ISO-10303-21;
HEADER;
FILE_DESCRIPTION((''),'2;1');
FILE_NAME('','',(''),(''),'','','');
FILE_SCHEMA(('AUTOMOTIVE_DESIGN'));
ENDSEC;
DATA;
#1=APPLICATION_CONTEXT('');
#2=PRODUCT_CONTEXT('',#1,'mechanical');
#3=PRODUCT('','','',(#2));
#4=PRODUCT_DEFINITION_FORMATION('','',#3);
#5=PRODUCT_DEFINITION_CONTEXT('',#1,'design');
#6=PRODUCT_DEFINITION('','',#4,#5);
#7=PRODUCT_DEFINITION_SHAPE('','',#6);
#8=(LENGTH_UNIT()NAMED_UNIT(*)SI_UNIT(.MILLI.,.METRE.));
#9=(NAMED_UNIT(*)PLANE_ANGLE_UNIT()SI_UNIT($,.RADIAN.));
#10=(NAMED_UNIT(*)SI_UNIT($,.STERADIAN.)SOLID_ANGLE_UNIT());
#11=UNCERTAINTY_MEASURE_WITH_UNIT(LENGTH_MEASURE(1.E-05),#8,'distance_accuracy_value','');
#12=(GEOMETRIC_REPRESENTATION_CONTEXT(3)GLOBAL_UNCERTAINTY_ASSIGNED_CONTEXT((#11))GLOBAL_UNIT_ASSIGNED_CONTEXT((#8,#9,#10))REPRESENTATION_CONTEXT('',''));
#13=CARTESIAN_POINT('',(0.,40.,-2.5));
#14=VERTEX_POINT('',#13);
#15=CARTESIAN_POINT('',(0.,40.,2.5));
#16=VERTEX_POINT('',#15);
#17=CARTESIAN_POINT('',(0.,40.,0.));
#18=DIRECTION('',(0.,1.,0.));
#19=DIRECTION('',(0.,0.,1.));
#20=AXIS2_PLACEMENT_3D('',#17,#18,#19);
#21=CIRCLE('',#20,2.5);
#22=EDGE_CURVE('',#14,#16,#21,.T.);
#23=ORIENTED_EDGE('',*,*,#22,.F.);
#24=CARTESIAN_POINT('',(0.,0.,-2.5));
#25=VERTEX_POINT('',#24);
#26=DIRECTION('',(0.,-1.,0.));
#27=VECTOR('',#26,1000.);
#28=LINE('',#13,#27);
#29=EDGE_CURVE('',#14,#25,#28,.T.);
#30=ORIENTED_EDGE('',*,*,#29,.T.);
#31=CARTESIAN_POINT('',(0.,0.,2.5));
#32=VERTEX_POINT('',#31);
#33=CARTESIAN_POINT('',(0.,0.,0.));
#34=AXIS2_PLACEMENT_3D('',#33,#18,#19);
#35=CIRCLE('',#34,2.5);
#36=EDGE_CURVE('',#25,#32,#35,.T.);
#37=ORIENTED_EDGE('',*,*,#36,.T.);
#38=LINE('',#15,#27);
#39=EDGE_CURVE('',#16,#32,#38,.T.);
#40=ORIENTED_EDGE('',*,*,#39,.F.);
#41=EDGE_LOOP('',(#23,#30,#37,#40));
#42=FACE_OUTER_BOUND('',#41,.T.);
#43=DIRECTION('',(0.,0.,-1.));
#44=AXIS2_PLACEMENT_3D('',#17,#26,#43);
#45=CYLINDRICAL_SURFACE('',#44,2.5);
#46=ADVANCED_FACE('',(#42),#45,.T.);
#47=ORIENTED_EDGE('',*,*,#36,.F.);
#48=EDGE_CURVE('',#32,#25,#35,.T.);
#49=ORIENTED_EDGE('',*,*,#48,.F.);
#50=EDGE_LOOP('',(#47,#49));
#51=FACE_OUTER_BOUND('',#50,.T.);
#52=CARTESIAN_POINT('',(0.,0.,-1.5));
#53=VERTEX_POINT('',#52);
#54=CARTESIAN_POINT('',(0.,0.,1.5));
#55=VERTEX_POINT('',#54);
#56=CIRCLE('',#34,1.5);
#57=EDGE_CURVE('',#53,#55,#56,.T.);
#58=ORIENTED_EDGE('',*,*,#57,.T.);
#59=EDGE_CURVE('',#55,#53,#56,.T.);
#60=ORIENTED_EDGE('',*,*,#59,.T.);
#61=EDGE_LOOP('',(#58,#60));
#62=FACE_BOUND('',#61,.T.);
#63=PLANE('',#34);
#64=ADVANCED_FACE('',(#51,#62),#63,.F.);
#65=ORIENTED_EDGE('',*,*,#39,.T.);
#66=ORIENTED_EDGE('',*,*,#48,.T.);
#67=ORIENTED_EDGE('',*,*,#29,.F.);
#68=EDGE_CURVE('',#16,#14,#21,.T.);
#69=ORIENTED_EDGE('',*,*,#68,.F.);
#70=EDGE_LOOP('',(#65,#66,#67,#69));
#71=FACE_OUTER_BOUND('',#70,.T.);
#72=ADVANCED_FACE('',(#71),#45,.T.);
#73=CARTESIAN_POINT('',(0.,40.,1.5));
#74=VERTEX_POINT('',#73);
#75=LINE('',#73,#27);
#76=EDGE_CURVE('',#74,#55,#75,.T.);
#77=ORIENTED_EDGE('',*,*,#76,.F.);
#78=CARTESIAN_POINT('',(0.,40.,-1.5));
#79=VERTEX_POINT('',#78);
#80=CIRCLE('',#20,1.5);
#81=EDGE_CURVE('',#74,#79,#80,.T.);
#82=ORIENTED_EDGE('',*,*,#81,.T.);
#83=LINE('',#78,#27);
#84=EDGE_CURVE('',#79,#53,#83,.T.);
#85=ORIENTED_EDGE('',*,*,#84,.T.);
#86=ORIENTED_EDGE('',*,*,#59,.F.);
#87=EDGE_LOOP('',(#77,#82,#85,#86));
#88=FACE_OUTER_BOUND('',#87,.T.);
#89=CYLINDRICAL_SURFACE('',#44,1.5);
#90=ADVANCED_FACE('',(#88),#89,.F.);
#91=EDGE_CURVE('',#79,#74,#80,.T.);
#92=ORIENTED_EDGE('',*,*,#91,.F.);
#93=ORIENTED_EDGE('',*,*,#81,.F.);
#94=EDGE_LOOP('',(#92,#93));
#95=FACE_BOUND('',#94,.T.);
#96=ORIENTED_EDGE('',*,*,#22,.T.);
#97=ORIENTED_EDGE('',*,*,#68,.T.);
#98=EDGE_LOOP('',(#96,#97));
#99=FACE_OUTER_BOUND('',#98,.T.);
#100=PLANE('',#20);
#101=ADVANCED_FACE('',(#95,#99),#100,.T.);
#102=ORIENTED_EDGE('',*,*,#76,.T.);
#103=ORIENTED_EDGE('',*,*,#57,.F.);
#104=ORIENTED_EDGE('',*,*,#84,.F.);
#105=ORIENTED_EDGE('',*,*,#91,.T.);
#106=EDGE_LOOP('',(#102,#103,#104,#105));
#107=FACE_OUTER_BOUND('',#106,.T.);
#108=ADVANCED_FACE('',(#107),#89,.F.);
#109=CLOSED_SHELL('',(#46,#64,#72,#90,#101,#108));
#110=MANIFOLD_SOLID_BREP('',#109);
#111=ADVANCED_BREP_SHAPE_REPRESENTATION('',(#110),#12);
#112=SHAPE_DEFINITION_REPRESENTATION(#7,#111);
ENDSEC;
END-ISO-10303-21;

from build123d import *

# Parameters (mm, degrees)
SKETCH_1_R      = 2.5
SKETCH_1_R_2    = 1.5
EXTRUDE_1_DEPTH = 40


with BuildPart() as part:
    # 草图1 → 凸台-拉伸1 (new body)
    with BuildSketch(Plane(origin=(0, 0, 0), x_dir=(1, 0, 0), z_dir=(0, 1, 0))):
        with Locations(Location((0, 0, 0), (0, 0, 270))):
            Circle(SKETCH_1_R)
        with Locations(Location((0, 0, 0), (0, 0, 270))):
            Circle(SKETCH_1_R_2, mode=Mode.SUBTRACT)
    extrude(amount=EXTRUDE_1_DEPTH)


solid = part.part
